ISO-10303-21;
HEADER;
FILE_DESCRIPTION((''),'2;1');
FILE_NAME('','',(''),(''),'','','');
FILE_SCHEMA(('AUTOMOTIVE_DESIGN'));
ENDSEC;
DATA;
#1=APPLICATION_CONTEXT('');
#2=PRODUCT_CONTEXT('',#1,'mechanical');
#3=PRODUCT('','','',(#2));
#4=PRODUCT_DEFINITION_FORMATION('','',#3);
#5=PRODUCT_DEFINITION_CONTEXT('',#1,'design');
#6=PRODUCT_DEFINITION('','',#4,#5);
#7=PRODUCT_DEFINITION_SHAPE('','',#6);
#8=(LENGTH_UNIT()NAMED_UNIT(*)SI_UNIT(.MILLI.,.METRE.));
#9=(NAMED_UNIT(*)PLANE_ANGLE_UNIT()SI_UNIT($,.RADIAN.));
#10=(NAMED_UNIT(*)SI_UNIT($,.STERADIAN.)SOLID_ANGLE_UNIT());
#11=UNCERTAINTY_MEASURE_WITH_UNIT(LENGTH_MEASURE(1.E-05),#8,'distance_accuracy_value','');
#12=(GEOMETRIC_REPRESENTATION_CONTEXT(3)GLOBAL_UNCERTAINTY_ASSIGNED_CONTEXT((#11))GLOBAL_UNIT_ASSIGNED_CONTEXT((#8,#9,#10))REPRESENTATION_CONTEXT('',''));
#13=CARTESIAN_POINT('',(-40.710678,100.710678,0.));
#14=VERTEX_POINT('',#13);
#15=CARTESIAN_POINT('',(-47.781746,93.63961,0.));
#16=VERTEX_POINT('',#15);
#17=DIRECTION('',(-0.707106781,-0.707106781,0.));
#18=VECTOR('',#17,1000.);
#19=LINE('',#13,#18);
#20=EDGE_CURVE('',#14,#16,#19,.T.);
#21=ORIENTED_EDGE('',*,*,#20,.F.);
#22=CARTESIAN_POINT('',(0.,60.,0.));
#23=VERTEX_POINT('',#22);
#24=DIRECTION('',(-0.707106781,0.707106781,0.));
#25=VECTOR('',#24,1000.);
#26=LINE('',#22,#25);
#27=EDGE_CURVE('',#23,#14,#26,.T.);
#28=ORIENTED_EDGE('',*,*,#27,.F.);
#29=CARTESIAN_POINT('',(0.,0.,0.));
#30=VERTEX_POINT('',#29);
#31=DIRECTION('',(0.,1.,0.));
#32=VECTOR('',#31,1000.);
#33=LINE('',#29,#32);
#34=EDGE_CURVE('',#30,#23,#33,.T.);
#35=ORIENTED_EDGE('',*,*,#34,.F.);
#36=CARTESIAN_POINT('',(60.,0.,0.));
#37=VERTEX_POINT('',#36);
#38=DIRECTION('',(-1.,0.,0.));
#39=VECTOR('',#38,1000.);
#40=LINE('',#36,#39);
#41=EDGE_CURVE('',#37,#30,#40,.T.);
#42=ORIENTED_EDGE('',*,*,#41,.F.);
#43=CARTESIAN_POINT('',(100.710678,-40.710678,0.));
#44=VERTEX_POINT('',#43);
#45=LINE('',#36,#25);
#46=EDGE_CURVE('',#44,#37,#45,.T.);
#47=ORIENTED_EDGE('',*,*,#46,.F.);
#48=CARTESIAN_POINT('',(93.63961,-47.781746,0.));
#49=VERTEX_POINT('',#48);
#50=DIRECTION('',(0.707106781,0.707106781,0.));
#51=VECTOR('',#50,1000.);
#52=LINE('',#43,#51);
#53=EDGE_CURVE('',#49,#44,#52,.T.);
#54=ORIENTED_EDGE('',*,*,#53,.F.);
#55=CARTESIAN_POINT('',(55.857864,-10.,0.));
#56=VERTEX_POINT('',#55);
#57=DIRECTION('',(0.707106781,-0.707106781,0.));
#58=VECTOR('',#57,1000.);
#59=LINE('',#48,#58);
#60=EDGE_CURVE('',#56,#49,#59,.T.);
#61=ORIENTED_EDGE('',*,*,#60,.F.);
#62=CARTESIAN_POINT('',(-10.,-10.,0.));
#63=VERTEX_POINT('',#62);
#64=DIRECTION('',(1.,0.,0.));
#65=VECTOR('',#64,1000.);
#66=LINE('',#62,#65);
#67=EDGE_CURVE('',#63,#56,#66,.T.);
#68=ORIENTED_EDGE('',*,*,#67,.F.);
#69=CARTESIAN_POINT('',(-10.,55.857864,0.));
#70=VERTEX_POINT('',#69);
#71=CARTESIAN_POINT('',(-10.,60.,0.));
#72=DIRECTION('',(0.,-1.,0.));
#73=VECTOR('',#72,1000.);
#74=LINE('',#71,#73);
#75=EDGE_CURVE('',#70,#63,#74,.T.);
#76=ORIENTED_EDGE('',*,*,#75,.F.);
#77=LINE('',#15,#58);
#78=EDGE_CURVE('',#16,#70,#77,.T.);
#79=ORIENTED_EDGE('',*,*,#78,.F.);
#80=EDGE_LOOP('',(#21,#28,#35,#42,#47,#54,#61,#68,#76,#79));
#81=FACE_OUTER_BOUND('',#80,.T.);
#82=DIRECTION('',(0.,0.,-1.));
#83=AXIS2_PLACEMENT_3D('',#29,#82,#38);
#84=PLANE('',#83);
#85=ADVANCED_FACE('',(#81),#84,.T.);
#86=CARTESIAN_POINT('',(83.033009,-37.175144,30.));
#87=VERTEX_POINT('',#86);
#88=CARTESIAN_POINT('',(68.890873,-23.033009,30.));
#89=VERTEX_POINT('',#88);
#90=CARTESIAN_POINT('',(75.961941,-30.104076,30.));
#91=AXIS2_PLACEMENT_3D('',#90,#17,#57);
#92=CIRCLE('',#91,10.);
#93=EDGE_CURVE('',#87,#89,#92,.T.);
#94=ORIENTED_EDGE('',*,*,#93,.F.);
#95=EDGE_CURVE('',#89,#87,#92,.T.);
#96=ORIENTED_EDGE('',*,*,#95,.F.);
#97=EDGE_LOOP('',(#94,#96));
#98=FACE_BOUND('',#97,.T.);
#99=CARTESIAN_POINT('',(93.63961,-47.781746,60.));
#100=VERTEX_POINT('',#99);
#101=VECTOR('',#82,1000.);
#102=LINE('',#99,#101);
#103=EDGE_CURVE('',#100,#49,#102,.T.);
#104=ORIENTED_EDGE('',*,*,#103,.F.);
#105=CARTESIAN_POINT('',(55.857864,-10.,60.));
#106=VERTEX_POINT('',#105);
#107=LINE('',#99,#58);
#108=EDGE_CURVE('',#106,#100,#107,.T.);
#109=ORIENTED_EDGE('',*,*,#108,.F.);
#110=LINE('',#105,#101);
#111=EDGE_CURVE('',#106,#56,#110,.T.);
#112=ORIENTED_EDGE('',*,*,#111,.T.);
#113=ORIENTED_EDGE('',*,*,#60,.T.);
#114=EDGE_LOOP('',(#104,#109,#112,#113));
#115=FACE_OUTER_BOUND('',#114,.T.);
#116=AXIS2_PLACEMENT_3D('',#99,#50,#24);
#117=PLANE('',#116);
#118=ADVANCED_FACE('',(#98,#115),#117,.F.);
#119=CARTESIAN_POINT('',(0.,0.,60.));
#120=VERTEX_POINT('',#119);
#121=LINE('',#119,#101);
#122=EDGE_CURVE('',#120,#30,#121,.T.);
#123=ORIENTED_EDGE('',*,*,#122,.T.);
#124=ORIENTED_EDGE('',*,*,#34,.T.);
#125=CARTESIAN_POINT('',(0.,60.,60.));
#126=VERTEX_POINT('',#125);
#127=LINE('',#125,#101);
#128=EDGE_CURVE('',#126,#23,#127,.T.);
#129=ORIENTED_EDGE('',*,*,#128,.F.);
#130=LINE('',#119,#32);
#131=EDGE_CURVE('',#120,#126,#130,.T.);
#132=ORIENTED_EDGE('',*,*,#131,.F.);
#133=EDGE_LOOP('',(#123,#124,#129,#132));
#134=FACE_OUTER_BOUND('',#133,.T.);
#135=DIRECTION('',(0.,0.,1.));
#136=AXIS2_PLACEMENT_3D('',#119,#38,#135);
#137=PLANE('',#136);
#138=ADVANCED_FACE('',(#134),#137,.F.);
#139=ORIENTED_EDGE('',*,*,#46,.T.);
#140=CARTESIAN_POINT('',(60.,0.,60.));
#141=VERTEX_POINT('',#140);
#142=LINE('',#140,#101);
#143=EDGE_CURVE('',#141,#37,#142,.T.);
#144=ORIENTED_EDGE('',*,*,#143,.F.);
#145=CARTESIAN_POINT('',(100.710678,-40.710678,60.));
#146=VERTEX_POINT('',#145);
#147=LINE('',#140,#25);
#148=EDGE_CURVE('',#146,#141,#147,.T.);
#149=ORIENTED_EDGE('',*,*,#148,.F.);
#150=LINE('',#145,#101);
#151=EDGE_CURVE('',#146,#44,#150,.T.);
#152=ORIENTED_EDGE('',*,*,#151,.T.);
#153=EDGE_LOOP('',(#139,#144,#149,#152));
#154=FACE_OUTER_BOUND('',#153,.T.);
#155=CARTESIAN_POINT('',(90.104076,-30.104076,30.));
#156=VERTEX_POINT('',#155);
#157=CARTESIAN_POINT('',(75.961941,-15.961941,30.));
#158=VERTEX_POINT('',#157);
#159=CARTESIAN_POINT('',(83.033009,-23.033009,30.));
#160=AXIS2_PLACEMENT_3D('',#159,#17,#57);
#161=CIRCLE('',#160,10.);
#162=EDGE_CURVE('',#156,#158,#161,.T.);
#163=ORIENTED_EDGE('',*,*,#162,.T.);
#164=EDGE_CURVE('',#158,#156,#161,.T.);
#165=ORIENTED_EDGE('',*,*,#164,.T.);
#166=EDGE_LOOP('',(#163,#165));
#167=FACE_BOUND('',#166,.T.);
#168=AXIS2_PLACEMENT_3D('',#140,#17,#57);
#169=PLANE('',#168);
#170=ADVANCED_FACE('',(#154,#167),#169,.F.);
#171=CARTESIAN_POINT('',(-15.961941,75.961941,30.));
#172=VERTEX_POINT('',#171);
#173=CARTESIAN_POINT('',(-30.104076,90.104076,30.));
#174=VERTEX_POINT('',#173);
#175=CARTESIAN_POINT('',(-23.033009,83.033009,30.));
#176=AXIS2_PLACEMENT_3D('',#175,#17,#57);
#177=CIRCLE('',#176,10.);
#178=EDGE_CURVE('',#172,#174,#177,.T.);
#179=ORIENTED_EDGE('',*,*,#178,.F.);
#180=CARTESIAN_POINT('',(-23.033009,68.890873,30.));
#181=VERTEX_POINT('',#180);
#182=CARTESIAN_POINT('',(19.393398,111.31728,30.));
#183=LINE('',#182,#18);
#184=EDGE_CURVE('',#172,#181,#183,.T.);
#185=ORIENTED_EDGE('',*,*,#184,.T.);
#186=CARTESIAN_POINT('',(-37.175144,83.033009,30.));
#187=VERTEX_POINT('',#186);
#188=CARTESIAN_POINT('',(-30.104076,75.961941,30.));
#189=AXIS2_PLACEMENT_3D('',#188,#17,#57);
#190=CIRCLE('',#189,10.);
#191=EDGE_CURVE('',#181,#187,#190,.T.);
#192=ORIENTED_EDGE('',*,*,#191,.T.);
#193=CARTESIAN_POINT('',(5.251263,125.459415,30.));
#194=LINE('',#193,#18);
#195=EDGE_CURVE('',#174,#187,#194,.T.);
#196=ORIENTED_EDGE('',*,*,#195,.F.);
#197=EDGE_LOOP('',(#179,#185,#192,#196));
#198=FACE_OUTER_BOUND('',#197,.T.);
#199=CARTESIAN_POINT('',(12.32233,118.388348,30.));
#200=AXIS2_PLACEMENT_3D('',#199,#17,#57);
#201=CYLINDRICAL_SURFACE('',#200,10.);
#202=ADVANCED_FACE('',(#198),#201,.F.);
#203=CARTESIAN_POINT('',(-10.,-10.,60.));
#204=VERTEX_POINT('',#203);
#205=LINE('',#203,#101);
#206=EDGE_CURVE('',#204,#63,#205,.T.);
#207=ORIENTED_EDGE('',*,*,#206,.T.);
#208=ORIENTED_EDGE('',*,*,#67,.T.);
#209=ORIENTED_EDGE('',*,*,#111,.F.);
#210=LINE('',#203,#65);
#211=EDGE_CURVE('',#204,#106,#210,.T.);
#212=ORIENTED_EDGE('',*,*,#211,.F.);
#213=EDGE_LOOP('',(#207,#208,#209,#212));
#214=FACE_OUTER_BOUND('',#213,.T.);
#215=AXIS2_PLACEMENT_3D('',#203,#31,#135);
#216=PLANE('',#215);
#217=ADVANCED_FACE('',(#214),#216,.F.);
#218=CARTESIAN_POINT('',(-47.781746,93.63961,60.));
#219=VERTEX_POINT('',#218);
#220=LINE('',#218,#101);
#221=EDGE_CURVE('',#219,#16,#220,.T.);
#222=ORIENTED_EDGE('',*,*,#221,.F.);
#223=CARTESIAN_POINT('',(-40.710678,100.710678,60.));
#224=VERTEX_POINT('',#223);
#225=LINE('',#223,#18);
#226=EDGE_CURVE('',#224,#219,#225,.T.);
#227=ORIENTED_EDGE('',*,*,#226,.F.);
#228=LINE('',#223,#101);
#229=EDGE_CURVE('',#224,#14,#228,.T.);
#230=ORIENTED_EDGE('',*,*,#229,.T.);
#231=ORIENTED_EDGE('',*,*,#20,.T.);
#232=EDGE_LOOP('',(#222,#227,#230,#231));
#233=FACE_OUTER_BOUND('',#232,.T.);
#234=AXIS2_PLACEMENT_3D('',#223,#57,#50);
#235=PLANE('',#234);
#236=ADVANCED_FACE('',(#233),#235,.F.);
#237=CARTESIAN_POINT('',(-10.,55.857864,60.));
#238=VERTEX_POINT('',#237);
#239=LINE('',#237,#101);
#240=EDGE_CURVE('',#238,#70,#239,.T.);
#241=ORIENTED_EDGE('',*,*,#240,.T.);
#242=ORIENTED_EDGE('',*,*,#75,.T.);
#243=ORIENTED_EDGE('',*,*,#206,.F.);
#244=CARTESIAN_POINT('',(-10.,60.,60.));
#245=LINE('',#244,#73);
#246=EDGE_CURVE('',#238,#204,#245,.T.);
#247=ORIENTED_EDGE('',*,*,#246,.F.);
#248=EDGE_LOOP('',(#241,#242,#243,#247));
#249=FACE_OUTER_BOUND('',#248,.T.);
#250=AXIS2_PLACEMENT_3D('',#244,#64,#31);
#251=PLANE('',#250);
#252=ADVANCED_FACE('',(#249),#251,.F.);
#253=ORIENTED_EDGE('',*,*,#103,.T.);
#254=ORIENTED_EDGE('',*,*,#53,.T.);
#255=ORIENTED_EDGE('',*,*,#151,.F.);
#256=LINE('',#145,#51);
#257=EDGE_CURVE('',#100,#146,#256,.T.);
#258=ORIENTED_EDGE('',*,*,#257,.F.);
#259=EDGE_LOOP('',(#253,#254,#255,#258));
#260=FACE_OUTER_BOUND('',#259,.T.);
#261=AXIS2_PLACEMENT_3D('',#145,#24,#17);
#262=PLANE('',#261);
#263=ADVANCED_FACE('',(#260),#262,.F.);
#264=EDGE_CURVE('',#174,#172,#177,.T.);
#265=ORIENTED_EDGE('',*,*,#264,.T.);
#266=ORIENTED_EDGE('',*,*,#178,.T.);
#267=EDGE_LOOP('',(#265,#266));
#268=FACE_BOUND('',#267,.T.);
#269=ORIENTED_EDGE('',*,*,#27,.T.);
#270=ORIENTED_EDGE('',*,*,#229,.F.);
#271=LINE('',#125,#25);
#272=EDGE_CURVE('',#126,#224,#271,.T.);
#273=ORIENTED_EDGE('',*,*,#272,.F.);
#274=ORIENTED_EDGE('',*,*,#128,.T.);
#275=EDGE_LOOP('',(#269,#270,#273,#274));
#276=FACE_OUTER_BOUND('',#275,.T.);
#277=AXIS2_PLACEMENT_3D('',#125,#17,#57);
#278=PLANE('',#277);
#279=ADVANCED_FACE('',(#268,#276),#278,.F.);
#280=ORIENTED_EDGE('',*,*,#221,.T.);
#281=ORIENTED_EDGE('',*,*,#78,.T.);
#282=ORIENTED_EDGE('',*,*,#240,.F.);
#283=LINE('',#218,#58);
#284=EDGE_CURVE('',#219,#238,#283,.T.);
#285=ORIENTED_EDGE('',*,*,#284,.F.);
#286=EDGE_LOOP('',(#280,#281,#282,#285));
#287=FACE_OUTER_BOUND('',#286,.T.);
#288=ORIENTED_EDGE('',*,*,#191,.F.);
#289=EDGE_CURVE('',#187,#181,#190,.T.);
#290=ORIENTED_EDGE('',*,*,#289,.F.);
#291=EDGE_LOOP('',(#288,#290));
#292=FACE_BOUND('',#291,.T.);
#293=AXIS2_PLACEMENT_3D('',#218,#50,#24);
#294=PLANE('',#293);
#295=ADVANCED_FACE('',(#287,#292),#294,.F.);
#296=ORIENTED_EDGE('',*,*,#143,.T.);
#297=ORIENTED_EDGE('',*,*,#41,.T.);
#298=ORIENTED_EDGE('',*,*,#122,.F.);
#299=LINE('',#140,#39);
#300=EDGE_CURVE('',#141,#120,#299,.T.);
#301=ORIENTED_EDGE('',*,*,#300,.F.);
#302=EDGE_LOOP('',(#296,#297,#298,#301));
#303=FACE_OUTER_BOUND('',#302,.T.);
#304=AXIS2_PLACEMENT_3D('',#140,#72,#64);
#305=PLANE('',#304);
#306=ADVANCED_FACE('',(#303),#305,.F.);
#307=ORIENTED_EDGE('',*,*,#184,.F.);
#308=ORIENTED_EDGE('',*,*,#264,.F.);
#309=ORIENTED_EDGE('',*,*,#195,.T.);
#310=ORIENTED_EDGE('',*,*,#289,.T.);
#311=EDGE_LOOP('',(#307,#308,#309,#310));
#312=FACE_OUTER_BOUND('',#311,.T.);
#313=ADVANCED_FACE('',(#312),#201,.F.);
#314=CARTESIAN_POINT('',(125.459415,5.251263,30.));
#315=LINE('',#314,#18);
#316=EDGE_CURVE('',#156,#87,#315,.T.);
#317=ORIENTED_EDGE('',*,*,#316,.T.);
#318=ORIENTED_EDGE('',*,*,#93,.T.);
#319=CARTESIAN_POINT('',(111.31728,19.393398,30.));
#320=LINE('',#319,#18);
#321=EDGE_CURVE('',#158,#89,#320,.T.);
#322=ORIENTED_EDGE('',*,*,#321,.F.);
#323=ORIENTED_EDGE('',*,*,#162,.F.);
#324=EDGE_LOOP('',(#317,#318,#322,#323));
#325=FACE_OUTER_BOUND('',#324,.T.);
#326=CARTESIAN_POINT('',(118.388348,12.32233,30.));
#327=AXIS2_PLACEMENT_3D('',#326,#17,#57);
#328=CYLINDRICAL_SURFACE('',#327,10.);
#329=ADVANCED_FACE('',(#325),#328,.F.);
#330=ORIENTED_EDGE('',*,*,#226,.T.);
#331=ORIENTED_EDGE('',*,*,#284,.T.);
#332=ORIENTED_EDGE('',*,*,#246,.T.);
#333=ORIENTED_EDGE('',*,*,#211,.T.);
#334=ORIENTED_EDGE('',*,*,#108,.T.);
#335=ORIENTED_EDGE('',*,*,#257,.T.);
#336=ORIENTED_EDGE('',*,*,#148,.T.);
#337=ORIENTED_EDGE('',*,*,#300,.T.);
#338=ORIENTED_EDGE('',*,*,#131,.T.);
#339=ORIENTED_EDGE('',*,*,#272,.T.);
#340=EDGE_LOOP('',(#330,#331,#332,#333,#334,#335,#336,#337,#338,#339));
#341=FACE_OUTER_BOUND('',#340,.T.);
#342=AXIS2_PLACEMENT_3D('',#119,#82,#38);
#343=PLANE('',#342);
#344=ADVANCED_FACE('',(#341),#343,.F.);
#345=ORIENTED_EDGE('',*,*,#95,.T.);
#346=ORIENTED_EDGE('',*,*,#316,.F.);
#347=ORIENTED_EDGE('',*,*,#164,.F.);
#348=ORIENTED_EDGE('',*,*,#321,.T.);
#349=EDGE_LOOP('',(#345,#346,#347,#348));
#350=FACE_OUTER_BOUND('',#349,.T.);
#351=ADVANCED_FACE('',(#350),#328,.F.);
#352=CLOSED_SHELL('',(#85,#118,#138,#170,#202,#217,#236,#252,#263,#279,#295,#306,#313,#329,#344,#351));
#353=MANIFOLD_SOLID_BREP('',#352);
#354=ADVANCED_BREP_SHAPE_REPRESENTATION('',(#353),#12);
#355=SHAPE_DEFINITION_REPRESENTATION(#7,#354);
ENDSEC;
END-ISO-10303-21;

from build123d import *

# Parameters (mm, degrees)
EXTRUDE_1_DEPTH     = 60
EXTRUDE_2_DEPTH     = 60
SKETCH_3_R          = 10
CUT_EXTRUDE_1_DEPTH = 60


with BuildPart() as part:
    # 草图1 → 凸台-拉伸1 (new body)
    with BuildSketch(Plane.XY):
        Polygon((0, 0), (0, 60), (-10, 60), (-10, -10), (60, -10), (60, 0), align=None)
    extrude(amount=EXTRUDE_1_DEPTH)

    # 草图2 → 凸台-拉伸2 (add)
    with BuildSketch(Plane.XY):
        Polygon((0, 60), (-40.710678119, 100.710678119), (-47.781745931, 93.639610307), (-10, 55.857864376), (-10, 60), align=None)
        Polygon((60, 0), (100.710678119, -40.710678119), (93.639610307, -47.781745931), (55.857864376, -10), (60, -10), align=None)
    extrude(amount=EXTRUDE_2_DEPTH)

    # 草图3 → 切除-拉伸1 (cut)
    with BuildSketch(Plane(origin=(22.928932188, 22.928932188, 0), x_dir=(0, 0, 1), z_dir=(-0.7071067811865501, -0.7071067811865449, 0))):
        with Locations(Location((30, 75, 0), (0, 0, 270))):
            Circle(SKETCH_3_R)
        with Locations(Location((30, -75, 0), (0, 0, 270))):
            Circle(SKETCH_3_R)
    extrude(amount=-CUT_EXTRUDE_1_DEPTH, mode=Mode.SUBTRACT)


solid = part.part
